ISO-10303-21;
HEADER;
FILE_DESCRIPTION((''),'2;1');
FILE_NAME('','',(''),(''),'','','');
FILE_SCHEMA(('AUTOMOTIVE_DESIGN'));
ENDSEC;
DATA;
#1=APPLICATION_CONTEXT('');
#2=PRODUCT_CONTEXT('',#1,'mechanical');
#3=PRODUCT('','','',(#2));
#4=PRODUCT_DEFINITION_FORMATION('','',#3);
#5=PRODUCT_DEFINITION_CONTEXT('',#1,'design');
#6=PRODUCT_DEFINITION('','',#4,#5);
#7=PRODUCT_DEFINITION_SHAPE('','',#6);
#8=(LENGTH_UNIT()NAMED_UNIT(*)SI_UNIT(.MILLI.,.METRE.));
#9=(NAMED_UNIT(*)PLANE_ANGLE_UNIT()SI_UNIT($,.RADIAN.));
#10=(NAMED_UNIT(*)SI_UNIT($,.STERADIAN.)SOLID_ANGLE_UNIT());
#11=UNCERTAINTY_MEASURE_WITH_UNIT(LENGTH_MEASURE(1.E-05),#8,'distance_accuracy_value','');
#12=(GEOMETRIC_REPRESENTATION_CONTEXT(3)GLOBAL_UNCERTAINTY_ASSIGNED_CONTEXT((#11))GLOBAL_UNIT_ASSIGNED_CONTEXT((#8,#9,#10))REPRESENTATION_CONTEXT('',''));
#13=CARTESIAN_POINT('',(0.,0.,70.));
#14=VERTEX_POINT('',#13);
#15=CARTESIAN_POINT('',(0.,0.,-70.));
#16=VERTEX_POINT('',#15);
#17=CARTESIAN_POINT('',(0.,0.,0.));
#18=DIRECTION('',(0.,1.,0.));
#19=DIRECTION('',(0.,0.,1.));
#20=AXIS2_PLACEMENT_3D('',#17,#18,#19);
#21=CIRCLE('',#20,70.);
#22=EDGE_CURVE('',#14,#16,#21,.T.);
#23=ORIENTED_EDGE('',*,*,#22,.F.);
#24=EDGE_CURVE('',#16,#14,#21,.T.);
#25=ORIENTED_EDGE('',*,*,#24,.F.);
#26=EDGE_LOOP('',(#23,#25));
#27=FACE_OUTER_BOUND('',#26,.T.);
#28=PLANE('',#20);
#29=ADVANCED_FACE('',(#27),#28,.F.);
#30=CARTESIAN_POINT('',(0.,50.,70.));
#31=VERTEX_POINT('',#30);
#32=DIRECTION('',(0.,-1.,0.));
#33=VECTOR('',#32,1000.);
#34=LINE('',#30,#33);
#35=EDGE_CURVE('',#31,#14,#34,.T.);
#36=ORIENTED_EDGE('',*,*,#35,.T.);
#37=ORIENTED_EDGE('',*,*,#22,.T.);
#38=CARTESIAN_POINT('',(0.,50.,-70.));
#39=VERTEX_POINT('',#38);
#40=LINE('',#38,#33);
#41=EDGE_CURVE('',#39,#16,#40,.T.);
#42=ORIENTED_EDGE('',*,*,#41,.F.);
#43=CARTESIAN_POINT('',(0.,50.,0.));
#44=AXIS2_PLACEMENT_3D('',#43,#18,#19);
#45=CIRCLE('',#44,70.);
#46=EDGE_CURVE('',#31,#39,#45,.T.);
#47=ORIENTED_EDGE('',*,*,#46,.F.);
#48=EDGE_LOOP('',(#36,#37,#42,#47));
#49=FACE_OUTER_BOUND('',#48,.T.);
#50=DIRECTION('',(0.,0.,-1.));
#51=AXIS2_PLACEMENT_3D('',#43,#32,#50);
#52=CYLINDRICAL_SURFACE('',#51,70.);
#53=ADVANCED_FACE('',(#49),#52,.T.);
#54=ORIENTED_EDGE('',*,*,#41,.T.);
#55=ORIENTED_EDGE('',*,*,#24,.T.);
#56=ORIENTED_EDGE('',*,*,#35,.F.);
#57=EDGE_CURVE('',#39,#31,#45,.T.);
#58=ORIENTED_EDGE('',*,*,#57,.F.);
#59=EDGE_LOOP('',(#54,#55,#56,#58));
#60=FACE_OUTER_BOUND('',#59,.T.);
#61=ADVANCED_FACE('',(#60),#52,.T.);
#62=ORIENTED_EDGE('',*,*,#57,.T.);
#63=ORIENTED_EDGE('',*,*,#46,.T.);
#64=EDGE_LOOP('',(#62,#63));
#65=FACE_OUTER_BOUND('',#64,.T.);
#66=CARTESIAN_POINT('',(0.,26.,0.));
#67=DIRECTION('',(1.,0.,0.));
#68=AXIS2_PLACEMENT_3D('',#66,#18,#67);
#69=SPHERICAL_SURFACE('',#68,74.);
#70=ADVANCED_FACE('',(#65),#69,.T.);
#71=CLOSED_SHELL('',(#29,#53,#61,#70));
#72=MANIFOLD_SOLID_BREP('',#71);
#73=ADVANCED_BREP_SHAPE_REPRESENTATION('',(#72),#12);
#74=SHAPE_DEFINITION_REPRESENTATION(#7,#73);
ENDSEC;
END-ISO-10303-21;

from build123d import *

# Parameters (mm, degrees)
SKETCH1_R           = 70
BOSS_EXTRUDE1_DEPTH = 50
DOME1_FACE_RADIUS   = 70
DOME1_HEIGHT        = 50


with BuildPart() as part:
    # Sketch1 → Boss-Extrude1 (new body)
    with BuildSketch(Plane(origin=(0, 0, 0), x_dir=(1, 0, 0), z_dir=(0, 1, 0))):
        with Locations(Location((0, 0, 0), (0, 0, 270))):
            Circle(SKETCH1_R)
    extrude(amount=BOSS_EXTRUDE1_DEPTH)

    # Dome1: a dome of height H over a round flat face of radius A is a cap of a sphere of radius (A * A + H * H) / (2 * H)
    dome1_r = (DOME1_FACE_RADIUS * DOME1_FACE_RADIUS + DOME1_HEIGHT * DOME1_HEIGHT) / (2 * DOME1_HEIGHT)
    dome1_base = Plane((0, 50, 0), z_dir=(0, 1, 0))
    with Locations(dome1_base.offset(DOME1_HEIGHT - dome1_r)):
        dome1_ball = Sphere(dome1_r, mode=Mode.PRIVATE)
    add(split(dome1_ball, bisect_by=dome1_base, keep=Keep.TOP, mode=Mode.PRIVATE))


solid = part.part
